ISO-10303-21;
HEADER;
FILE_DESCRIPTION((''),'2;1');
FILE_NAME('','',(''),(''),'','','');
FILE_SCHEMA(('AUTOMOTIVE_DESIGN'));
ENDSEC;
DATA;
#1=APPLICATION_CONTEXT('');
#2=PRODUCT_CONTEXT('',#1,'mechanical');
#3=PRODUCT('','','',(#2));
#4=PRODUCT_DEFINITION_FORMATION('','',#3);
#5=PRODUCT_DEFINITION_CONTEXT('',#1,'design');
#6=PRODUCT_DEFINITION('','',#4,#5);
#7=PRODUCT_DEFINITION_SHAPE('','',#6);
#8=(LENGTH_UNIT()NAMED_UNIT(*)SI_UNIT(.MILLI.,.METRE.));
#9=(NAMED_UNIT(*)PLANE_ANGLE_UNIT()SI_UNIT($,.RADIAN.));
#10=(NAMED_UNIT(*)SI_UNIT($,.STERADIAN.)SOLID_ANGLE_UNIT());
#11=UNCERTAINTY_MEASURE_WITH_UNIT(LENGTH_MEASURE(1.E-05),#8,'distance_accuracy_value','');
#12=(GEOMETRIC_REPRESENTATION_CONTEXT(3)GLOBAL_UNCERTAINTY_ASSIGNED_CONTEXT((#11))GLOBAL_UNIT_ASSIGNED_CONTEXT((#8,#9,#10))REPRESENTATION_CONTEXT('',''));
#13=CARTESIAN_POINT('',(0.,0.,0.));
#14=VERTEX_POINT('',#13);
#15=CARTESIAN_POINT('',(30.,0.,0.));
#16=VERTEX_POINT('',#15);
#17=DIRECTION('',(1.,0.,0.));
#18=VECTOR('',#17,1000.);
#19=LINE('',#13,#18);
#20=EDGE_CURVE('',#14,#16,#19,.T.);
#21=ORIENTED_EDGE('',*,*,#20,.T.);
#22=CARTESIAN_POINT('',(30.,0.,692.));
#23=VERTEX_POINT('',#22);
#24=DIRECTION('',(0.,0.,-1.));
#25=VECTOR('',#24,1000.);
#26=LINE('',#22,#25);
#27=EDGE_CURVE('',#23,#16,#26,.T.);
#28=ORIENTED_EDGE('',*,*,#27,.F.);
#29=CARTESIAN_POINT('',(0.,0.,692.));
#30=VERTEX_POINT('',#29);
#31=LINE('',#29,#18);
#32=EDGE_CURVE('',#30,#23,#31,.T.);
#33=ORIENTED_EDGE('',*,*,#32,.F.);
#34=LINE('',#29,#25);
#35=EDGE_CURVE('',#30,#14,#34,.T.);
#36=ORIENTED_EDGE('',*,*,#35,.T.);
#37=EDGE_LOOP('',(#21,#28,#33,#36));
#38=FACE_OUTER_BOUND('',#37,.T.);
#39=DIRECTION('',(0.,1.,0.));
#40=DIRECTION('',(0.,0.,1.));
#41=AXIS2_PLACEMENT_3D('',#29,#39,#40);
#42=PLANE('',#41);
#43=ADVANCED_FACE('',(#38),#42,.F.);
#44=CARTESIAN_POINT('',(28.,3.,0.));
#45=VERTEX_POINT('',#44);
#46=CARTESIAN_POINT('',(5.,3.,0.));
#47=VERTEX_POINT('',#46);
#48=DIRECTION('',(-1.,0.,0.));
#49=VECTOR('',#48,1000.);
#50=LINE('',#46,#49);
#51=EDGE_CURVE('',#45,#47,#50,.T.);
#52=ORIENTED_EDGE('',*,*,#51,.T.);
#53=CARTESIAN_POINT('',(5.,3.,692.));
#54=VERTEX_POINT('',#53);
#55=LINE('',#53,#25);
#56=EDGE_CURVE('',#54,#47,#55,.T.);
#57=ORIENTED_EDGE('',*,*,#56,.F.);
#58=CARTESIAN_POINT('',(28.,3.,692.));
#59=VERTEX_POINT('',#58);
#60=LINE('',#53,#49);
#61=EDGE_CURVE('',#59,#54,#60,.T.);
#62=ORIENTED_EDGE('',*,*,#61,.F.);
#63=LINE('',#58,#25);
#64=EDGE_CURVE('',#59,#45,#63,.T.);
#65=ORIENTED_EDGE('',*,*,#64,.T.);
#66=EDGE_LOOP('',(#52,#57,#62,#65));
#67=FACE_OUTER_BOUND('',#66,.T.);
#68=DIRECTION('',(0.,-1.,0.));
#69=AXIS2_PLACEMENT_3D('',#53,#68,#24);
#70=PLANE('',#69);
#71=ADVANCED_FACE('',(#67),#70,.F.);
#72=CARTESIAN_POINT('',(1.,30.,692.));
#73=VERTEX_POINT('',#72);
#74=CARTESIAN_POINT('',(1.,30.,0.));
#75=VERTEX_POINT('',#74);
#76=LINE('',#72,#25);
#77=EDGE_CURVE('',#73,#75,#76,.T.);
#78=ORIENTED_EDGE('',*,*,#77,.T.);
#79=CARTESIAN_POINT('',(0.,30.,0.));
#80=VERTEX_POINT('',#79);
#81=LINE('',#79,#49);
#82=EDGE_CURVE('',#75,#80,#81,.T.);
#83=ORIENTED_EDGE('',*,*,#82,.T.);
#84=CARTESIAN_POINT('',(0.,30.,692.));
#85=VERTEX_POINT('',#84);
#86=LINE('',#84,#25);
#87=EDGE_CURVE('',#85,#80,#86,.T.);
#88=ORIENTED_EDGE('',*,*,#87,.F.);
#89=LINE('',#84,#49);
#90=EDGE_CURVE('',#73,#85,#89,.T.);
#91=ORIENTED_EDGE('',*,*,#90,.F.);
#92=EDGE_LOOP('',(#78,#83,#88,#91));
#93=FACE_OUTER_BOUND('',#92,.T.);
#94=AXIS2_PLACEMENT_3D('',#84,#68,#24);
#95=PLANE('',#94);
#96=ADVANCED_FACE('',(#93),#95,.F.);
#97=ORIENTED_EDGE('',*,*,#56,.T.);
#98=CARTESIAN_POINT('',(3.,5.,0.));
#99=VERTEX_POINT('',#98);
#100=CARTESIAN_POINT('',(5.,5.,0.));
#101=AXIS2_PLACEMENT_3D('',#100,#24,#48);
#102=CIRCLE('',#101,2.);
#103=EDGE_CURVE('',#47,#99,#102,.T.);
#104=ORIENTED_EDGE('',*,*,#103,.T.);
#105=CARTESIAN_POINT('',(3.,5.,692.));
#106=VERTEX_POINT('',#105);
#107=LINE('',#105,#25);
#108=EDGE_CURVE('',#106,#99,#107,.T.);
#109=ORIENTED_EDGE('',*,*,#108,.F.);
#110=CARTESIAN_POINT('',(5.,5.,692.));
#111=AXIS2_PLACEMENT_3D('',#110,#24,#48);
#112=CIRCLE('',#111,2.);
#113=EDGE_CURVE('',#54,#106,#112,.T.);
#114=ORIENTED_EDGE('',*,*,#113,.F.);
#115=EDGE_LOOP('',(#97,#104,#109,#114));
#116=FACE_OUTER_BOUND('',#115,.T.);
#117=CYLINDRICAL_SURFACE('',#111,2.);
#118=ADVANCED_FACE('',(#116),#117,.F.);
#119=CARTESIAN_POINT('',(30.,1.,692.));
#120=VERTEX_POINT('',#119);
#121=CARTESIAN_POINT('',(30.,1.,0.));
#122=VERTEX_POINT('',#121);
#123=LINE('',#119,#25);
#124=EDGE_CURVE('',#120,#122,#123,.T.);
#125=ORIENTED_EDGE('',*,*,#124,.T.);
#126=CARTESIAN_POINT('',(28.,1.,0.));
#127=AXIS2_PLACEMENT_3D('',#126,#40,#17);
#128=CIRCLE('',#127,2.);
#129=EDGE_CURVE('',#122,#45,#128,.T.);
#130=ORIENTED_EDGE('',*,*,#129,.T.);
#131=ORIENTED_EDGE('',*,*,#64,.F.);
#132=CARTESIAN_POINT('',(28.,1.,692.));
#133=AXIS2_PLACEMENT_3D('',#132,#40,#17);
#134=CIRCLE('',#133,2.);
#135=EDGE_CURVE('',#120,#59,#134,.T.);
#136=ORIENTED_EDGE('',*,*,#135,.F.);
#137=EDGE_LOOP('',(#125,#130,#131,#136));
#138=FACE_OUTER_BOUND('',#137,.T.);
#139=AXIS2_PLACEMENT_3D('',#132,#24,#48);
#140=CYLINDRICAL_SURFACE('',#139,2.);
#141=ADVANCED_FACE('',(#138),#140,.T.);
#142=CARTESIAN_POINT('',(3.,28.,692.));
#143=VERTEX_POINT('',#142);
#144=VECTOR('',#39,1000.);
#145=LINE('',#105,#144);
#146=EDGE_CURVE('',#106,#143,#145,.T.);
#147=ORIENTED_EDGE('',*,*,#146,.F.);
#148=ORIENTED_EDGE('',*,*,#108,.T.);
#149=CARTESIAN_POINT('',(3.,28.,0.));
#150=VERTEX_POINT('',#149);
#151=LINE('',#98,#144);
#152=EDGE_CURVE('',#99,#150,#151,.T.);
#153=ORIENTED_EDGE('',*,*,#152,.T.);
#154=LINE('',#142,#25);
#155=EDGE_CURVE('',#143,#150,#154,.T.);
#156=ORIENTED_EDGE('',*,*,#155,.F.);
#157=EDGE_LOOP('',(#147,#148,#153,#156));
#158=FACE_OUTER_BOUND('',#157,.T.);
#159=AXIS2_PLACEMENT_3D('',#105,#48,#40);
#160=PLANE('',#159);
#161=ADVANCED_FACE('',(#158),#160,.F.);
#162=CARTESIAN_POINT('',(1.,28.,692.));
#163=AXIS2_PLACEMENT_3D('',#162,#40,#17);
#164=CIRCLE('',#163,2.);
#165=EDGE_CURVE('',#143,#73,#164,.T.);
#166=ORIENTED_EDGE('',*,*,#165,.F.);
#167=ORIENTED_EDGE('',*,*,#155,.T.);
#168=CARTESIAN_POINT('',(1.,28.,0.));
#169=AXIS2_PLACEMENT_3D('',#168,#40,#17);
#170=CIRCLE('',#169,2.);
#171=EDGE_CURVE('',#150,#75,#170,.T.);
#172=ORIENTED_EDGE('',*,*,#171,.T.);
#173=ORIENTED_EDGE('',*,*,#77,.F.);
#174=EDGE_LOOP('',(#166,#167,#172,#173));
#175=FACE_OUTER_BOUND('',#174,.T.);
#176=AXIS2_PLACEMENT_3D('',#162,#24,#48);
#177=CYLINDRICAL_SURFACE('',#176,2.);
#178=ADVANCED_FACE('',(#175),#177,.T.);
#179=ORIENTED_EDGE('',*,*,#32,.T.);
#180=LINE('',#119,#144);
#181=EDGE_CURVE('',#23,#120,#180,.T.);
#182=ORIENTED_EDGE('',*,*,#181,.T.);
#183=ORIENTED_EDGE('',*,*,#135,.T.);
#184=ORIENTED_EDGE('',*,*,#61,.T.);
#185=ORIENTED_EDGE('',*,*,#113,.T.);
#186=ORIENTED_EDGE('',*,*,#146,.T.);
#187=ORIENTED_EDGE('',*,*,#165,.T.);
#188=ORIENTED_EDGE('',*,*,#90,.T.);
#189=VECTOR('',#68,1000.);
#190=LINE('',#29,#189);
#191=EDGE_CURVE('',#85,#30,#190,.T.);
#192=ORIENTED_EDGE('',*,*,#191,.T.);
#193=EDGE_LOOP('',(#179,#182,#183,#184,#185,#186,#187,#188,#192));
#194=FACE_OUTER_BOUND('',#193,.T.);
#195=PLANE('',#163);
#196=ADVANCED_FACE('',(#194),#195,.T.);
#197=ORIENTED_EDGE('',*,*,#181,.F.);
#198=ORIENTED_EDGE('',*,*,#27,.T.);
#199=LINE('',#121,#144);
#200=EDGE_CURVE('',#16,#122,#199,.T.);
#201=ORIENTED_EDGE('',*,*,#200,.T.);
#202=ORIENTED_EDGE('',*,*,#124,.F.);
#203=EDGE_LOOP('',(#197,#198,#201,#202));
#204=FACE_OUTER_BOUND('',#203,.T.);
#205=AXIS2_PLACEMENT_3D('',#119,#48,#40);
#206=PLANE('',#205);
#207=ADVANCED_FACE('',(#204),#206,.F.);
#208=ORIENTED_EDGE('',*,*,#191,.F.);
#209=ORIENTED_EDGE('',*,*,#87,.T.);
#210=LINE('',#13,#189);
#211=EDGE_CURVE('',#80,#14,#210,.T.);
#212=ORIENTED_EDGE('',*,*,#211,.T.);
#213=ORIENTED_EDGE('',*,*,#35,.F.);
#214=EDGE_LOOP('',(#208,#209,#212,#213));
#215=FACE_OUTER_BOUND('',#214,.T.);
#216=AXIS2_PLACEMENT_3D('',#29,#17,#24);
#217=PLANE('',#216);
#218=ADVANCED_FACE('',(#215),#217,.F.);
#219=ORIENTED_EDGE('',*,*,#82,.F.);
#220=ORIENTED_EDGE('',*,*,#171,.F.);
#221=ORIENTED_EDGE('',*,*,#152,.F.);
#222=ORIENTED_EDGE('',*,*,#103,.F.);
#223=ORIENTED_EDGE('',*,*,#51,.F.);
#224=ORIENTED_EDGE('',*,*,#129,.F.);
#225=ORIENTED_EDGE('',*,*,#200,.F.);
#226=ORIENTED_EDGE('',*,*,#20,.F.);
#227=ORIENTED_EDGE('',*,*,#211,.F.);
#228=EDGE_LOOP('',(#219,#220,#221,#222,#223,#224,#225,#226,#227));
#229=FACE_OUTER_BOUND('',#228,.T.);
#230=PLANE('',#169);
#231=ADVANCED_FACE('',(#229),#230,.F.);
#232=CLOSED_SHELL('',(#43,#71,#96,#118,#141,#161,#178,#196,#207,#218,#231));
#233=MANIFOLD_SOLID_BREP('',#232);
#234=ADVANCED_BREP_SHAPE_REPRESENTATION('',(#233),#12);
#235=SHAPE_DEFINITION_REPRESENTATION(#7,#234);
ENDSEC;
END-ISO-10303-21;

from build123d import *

# Parameters (mm, degrees)
BOSS_EXTRUDE1_DEPTH = 692


with BuildPart() as part:
    # Sketch1 → Boss-Extrude1 (new body)
    with BuildSketch(Plane.XY):
        with BuildLine():
            Line((0, 0), (30, 0))
            Line((30, 0), (30, 1))
            ThreePointArc((30, 1), (29.414213562, 2.414213562), (28, 3))
            Line((28, 3), (5, 3))
            ThreePointArc((5, 3), (3.585786438, 3.585786438), (3, 5))
            Line((3, 5), (3, 28))
            ThreePointArc((3, 28), (2.414213562, 29.414213562), (1, 30))
            Line((1, 30), (0, 30))
            Line((0, 30), (0, 0))
        make_face()
    extrude(amount=BOSS_EXTRUDE1_DEPTH)


solid = part.part
